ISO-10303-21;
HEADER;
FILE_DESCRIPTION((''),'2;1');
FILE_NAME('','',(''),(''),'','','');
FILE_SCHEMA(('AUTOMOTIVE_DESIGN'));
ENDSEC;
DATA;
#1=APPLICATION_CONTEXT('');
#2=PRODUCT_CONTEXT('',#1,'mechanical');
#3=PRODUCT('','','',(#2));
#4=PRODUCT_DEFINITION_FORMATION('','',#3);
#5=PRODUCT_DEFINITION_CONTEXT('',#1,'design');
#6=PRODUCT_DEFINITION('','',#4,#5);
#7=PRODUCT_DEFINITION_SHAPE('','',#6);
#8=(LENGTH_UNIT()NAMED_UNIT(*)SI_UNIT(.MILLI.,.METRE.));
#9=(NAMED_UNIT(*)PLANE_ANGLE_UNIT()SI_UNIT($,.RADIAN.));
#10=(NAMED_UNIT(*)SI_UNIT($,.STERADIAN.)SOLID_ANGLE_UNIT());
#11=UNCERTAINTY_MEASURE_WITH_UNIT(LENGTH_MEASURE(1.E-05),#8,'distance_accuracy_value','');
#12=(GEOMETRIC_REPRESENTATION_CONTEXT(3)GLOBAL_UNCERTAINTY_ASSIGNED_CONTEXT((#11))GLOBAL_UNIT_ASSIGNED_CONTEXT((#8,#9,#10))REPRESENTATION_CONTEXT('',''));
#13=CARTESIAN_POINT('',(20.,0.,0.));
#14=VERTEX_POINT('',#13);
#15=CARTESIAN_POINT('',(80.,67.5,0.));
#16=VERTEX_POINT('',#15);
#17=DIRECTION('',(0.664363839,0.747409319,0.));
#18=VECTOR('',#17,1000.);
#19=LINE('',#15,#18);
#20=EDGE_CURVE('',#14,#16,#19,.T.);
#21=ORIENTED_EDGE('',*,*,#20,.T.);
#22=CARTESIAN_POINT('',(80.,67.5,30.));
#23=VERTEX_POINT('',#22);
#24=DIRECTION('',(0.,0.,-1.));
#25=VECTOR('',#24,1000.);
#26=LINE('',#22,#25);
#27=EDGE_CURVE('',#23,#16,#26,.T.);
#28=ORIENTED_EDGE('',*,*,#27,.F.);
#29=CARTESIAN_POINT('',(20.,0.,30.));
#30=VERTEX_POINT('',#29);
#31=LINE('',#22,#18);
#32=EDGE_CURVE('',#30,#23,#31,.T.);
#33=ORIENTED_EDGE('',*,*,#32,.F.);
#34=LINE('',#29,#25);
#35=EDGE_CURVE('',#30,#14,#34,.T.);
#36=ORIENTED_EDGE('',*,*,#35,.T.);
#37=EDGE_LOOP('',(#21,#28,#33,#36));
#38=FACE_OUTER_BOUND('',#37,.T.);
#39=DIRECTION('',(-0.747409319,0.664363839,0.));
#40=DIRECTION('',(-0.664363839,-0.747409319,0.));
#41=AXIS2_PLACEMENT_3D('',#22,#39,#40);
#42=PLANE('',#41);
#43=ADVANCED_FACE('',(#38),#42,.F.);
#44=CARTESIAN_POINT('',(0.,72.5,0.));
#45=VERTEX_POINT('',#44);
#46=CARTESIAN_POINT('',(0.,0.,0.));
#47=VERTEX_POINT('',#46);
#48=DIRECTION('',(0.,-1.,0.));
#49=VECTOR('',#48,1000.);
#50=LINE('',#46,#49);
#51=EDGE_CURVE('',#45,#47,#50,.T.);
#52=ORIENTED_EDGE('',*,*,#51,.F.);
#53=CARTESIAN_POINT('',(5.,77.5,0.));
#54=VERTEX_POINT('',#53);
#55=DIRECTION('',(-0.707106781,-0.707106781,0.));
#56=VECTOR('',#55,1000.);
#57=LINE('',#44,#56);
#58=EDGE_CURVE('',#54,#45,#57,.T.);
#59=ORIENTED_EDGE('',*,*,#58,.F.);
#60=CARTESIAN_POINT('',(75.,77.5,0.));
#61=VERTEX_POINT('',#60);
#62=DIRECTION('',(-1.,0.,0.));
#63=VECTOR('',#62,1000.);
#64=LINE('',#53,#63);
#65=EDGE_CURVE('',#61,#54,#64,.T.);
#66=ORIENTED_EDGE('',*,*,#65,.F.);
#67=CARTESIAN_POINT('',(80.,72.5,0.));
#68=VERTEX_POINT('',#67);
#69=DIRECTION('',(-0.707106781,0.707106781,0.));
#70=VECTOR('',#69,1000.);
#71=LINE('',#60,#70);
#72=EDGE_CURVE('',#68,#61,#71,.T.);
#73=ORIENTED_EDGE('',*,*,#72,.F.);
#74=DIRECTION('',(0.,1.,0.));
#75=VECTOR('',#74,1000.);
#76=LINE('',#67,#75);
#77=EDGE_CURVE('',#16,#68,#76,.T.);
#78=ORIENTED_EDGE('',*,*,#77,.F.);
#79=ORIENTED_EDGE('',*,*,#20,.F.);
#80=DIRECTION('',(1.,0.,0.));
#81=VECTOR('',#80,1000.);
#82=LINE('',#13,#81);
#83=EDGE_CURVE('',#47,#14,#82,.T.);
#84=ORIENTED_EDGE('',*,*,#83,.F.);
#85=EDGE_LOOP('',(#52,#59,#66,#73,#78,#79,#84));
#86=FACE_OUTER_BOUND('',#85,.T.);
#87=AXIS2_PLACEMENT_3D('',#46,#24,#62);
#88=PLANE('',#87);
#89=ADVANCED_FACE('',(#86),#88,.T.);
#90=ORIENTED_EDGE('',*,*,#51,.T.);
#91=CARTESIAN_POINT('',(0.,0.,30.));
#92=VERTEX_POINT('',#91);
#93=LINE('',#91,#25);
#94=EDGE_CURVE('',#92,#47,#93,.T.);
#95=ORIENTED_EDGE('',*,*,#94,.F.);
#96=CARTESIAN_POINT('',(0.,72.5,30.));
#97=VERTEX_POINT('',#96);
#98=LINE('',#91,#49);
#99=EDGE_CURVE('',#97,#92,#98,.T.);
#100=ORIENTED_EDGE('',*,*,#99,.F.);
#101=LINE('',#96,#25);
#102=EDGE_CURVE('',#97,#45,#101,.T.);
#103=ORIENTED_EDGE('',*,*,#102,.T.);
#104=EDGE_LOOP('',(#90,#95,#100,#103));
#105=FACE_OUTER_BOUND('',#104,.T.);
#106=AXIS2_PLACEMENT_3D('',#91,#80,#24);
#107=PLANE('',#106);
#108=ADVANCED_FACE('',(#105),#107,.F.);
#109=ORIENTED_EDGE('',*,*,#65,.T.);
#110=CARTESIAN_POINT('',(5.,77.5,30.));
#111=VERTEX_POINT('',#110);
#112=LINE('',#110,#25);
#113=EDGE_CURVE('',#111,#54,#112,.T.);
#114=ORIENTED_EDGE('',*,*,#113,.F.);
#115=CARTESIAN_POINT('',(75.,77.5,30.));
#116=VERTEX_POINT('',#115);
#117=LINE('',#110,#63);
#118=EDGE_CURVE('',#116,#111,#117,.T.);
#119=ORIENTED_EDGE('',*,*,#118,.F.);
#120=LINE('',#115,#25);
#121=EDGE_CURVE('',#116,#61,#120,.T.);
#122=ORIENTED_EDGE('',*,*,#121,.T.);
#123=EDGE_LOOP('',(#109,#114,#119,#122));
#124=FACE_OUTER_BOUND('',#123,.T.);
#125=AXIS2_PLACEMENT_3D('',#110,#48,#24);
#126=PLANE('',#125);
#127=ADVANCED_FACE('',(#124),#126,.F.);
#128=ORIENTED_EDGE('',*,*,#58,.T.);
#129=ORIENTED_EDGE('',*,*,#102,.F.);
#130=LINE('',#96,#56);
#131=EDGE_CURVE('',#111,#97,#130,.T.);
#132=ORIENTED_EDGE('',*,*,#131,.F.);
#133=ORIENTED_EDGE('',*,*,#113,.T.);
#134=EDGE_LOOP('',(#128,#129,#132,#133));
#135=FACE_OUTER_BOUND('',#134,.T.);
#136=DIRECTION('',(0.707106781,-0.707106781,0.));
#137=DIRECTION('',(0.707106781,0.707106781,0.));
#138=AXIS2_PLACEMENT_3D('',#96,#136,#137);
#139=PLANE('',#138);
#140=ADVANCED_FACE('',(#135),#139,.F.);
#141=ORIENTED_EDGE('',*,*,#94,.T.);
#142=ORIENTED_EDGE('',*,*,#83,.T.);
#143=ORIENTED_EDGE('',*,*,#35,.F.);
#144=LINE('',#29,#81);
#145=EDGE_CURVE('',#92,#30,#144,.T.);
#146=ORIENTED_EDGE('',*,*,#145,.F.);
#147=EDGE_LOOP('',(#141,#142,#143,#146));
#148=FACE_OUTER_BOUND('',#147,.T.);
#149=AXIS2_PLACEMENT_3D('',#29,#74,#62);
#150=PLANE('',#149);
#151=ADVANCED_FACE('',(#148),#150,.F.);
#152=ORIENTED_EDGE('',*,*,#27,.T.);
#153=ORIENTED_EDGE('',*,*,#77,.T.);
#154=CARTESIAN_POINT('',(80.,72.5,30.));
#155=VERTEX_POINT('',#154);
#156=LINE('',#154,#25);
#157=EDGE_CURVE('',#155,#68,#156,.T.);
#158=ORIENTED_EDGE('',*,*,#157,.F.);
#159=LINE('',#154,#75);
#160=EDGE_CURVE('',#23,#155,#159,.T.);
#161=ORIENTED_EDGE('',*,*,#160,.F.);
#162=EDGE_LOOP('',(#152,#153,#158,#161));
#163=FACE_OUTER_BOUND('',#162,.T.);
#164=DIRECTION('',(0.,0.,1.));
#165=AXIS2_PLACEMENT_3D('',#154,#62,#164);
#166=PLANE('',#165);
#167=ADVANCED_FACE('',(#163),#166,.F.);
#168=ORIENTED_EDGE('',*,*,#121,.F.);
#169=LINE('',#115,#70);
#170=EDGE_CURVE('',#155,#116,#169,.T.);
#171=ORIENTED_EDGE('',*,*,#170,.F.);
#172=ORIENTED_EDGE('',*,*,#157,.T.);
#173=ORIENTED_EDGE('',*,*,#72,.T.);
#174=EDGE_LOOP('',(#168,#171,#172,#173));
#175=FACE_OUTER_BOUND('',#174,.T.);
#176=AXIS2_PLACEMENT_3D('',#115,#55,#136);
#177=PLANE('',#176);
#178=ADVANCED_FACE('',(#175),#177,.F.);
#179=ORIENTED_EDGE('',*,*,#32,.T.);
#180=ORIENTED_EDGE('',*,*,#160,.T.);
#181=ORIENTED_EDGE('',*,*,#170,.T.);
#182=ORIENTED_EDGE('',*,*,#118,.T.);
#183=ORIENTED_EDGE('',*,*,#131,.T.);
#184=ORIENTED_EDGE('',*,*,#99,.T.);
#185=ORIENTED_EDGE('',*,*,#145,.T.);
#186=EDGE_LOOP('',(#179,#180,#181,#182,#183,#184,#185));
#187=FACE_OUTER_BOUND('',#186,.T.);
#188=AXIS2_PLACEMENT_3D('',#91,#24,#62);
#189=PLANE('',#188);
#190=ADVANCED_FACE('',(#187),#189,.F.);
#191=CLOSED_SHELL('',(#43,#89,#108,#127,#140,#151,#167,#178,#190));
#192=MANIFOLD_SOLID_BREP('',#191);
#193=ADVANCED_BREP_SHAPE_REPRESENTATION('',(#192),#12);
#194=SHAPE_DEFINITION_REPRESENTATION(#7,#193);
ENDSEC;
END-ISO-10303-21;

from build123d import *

# Parameters (mm, degrees)
BOSS_EXTRUDE1_DEPTH = 30


with BuildPart() as part:
    # Sketch1 → Boss-Extrude1 (new body)
    with BuildSketch(Plane.XY):
        Polygon((0, 0), (0, 72.5), (5, 77.5), (75, 77.5), (80, 72.5), (80, 67.5), (20, 0), align=None)
    extrude(amount=BOSS_EXTRUDE1_DEPTH)


solid = part.part
